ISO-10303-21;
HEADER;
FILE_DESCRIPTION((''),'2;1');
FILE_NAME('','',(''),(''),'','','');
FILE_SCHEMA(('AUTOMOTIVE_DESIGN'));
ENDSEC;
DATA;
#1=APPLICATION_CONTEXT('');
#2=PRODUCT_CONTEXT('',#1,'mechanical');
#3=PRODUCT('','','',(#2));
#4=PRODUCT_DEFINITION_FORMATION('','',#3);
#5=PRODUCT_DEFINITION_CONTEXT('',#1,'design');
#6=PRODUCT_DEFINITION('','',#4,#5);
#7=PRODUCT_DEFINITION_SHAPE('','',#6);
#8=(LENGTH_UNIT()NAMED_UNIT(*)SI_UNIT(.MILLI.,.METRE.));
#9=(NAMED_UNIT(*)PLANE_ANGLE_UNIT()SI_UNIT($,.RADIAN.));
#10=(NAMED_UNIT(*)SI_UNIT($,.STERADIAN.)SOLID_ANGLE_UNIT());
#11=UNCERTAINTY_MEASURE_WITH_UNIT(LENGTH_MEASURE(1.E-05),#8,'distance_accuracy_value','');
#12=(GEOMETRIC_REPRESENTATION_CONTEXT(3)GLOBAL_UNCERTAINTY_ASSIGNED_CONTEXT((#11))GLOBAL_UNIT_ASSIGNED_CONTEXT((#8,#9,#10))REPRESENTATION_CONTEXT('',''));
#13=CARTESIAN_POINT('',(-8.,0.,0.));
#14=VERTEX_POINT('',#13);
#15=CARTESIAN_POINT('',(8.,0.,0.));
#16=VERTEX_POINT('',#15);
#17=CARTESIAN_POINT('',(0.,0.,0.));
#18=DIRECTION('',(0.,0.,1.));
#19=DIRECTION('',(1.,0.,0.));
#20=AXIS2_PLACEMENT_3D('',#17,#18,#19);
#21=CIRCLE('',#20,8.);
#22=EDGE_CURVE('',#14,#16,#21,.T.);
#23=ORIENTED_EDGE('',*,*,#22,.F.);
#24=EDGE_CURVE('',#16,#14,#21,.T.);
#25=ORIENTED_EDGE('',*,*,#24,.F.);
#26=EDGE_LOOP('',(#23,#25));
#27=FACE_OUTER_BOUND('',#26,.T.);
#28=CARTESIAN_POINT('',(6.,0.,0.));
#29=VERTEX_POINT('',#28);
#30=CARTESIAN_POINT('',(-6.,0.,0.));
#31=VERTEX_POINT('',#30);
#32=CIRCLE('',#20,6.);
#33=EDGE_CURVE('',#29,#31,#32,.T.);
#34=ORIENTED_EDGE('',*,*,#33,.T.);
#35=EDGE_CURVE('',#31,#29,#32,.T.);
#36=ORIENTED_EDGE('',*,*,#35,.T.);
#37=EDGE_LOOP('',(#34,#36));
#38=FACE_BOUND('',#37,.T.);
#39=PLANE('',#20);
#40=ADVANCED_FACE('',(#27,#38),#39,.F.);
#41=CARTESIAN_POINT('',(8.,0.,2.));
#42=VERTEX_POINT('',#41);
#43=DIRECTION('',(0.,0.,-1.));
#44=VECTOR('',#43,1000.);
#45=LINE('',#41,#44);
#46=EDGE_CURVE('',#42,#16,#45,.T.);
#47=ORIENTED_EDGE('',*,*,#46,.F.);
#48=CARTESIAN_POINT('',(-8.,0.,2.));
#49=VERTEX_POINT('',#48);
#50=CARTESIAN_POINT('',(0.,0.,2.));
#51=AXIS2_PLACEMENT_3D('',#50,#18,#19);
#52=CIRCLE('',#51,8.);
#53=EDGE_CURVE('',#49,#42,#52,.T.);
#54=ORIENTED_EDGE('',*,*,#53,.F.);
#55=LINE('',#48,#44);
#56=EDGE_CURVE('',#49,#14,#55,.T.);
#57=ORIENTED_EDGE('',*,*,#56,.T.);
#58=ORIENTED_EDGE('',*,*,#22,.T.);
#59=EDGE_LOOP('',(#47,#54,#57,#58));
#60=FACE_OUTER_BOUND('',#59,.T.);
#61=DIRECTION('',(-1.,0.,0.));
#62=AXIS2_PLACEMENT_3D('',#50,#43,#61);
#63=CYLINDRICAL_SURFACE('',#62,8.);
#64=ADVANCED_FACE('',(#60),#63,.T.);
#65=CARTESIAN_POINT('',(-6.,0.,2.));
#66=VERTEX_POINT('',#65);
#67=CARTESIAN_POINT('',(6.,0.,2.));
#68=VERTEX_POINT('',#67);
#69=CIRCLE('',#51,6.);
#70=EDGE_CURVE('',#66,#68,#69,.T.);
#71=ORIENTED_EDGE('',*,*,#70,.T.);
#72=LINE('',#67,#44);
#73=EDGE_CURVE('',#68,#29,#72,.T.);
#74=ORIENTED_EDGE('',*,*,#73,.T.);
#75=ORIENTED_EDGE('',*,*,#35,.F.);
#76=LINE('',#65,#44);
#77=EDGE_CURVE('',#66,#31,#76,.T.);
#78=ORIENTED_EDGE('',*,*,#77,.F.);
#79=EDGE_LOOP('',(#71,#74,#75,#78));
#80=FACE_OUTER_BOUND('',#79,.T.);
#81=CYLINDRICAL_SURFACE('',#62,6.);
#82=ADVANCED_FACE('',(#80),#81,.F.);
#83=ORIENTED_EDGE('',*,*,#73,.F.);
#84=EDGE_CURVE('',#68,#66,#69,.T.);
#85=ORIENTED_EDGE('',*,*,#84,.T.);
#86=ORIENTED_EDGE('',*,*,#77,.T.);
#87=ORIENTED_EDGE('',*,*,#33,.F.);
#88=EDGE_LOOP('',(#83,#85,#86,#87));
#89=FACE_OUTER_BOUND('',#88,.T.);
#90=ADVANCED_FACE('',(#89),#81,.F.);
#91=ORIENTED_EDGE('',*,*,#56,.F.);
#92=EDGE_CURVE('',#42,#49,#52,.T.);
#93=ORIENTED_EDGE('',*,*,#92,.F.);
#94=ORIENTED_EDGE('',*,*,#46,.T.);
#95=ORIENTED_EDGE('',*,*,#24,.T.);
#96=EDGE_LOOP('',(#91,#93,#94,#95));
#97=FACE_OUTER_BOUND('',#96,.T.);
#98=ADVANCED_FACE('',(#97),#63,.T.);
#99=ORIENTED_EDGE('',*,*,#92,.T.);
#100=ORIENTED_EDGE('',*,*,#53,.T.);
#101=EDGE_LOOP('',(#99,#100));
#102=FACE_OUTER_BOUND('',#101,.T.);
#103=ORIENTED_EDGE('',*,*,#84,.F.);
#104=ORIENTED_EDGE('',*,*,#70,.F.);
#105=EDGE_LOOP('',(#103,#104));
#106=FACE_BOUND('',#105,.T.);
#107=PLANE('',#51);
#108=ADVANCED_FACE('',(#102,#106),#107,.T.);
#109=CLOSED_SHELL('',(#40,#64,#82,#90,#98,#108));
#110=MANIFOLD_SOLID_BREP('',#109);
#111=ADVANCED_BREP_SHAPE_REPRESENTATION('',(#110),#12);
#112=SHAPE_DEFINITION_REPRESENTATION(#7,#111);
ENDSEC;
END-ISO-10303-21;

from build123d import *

# Parameters (mm, degrees)
SKETCH1_R           = 8
SKETCH1_R_2         = 6
BOSS_EXTRUDE1_DEPTH = 2


with BuildPart() as part:
    # Sketch1 → Boss-Extrude1 (new body)
    with BuildSketch(Plane.XY):
        Circle(SKETCH1_R)
        Circle(SKETCH1_R_2, mode=Mode.SUBTRACT)
    extrude(amount=BOSS_EXTRUDE1_DEPTH)


solid = part.part
